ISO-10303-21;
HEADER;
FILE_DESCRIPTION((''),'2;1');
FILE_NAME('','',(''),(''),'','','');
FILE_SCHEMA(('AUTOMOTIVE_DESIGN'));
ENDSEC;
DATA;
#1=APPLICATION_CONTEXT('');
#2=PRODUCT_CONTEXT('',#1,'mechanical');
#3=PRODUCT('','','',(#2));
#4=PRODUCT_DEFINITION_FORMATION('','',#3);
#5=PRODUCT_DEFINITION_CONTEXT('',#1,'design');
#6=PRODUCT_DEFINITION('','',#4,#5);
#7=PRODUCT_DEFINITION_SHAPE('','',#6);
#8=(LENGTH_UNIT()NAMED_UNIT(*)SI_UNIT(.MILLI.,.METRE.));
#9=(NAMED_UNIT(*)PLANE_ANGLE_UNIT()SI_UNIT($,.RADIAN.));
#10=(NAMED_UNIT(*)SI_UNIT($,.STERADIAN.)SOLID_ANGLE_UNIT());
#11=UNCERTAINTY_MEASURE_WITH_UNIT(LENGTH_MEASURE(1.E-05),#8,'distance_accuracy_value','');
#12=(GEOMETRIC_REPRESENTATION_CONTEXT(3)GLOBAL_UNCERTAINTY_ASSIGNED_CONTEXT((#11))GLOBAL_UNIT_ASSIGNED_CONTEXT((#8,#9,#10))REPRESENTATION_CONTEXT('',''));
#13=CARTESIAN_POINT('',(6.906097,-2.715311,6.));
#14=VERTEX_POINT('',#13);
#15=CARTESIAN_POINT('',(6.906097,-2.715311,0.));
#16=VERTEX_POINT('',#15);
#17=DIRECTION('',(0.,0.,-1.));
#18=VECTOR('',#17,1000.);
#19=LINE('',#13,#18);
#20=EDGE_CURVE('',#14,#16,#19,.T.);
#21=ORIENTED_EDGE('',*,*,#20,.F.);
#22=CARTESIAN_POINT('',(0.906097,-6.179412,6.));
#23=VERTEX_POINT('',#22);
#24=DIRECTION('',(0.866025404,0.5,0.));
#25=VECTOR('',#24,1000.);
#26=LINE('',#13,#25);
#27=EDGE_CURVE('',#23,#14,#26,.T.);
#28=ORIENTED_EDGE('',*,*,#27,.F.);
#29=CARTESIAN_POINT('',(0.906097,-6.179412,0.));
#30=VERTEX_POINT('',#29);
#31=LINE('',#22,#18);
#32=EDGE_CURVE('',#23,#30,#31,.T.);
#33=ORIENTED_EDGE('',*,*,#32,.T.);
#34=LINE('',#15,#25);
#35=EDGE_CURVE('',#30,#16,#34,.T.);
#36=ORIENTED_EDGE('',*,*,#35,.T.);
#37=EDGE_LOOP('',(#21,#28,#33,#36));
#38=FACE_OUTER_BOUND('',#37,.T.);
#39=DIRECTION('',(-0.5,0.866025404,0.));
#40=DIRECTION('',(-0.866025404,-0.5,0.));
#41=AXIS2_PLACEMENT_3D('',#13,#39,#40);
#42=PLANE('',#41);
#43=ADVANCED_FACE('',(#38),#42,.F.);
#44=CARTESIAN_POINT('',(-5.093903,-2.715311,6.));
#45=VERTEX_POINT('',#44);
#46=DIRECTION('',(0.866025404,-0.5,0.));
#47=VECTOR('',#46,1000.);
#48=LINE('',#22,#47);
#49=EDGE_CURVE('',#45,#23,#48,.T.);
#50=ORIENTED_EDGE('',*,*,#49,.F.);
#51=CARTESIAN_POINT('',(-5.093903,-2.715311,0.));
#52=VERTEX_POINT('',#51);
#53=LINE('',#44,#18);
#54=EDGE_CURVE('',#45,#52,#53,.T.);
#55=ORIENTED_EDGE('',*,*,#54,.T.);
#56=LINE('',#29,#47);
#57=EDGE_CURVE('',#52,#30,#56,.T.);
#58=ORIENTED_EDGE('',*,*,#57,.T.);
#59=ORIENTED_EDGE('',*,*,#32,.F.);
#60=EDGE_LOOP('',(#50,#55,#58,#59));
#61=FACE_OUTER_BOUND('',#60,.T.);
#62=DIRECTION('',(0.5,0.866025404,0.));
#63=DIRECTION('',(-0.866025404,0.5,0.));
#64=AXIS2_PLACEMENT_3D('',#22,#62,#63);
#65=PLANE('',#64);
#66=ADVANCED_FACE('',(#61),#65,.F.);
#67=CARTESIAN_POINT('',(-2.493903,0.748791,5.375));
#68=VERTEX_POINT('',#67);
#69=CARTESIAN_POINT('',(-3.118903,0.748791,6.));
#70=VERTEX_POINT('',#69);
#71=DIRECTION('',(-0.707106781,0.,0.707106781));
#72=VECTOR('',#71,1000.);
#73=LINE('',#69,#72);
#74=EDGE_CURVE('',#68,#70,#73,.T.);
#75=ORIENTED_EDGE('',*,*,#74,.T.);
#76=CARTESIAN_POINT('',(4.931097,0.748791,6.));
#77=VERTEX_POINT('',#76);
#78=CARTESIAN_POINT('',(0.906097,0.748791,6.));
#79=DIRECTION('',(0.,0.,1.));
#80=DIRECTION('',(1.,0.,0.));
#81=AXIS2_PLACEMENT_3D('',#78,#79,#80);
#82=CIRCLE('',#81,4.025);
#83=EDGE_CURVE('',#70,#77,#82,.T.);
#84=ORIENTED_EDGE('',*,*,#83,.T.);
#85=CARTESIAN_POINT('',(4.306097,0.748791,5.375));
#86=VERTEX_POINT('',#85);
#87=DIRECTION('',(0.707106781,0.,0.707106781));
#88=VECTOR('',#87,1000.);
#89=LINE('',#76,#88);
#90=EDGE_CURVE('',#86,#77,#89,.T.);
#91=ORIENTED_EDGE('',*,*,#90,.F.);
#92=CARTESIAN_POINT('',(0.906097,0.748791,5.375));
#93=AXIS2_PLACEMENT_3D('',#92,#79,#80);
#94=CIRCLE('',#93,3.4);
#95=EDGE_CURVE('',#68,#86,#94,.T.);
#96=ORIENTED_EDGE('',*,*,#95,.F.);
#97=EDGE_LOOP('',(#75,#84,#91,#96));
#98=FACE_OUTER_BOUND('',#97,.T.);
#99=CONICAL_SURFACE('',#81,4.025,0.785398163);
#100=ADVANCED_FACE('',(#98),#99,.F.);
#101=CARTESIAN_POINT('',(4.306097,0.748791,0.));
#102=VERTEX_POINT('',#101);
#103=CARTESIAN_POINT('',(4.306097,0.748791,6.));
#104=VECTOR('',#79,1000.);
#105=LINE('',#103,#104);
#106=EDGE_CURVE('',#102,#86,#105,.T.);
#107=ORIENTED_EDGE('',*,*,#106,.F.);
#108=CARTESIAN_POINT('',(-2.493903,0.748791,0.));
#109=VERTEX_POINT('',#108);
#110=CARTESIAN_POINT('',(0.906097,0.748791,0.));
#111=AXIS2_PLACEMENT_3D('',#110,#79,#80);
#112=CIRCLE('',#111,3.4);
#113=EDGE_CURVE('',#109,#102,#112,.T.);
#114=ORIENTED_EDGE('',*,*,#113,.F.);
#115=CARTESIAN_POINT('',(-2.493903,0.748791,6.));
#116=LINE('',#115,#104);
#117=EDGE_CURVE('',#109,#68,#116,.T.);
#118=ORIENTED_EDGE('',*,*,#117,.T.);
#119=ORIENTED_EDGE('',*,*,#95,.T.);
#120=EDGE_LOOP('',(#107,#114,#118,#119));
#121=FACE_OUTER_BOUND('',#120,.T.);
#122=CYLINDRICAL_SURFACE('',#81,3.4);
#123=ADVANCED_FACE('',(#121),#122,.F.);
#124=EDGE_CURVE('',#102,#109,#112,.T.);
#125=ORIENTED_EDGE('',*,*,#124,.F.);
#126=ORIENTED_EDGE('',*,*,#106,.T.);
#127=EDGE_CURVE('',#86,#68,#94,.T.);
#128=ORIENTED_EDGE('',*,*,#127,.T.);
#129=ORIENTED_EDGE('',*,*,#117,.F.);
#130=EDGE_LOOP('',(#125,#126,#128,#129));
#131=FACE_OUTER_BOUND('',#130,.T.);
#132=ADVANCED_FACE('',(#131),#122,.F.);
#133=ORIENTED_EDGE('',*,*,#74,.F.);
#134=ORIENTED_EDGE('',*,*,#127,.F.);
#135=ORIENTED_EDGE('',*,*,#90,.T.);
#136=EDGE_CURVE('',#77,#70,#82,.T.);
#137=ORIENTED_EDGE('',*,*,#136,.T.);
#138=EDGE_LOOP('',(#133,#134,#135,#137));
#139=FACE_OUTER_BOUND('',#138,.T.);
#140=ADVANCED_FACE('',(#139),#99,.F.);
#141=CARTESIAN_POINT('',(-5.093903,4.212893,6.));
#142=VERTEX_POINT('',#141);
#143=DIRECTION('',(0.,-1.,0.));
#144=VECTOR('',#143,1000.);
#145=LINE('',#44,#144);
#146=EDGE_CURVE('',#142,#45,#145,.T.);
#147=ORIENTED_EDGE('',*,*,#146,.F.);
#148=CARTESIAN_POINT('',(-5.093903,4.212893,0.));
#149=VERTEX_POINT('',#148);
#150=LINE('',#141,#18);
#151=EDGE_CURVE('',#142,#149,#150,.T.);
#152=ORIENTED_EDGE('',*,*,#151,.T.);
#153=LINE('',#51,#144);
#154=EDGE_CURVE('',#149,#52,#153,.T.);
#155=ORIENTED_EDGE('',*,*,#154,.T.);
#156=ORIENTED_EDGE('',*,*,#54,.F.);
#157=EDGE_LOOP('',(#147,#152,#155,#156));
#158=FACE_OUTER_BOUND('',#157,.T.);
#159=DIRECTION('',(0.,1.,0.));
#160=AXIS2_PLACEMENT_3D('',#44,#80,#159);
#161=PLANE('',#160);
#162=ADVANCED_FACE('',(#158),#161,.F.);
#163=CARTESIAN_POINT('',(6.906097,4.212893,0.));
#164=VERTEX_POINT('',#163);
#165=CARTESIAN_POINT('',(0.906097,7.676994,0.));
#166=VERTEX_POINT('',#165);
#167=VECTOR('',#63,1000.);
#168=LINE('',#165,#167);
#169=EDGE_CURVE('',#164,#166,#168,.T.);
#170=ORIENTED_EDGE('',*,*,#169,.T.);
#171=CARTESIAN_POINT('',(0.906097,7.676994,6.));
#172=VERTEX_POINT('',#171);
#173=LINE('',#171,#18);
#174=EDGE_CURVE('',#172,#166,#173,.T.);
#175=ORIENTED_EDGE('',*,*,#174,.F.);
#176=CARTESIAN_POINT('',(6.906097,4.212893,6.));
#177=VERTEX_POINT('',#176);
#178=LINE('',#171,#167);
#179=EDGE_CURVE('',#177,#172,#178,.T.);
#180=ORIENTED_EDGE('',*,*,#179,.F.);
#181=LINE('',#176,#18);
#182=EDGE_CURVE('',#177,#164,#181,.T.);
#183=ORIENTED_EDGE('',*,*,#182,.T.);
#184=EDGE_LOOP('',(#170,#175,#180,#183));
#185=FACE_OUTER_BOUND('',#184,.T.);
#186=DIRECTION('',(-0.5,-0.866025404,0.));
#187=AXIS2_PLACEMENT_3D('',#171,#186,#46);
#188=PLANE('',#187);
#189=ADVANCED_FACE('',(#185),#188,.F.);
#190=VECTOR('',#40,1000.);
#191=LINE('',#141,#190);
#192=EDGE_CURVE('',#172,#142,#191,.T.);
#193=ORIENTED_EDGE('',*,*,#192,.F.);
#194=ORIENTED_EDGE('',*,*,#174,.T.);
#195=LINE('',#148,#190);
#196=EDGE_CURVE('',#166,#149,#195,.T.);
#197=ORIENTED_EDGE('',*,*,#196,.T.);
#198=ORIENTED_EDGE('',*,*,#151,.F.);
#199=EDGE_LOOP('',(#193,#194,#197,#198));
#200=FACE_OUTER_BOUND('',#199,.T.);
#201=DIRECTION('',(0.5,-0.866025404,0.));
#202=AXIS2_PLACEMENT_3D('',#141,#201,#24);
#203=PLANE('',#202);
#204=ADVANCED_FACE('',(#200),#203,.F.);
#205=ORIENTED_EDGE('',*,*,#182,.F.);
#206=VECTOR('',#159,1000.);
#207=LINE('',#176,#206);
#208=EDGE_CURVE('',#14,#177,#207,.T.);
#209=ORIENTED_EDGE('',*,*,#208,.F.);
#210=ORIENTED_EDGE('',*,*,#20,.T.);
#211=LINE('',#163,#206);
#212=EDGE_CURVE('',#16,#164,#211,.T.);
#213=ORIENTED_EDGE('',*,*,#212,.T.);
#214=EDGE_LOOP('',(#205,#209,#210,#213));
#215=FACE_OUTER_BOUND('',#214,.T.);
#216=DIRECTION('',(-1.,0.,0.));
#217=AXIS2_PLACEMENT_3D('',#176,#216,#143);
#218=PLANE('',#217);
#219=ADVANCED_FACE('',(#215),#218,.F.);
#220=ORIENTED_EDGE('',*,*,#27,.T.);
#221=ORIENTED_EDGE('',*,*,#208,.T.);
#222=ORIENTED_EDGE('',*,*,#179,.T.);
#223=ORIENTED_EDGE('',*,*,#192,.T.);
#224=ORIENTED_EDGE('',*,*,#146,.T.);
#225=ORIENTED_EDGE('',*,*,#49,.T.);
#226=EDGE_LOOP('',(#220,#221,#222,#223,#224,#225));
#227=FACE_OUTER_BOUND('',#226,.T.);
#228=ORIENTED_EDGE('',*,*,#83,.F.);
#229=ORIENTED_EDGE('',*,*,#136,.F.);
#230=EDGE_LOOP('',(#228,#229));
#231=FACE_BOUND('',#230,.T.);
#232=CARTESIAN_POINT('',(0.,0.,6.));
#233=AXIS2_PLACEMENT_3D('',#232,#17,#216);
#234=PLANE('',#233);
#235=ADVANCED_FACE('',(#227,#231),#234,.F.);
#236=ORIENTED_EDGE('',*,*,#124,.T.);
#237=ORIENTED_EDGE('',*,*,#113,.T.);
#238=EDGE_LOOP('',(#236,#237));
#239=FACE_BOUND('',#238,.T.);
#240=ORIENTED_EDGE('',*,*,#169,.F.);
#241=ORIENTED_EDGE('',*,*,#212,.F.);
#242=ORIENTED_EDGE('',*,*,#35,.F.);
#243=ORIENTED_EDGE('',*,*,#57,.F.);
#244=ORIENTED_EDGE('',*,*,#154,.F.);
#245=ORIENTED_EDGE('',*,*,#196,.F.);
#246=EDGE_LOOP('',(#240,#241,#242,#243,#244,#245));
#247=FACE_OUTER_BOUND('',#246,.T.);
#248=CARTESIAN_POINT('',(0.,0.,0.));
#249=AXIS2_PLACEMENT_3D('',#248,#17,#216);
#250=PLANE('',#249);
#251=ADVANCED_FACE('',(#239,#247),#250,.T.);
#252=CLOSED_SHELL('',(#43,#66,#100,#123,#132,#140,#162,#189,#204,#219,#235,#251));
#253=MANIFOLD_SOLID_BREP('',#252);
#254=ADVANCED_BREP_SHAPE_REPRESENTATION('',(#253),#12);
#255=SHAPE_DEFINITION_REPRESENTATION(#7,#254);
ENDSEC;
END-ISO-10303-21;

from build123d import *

# Parameters (mm, degrees)
BOSS_EXTRUDE1_DEPTH         = 6
M8_TAPPED_HOLE1_D           = 6.8
M8_TAPPED_HOLE1_CSINK_D     = 8.05
M8_TAPPED_HOLE1_CSINK_ANGLE = 90


with BuildPart() as part:
    # Sketch1 → Boss-Extrude1 (new body)
    with BuildSketch(Plane.XY):
        Polygon((-5.093902669, -2.715310597), (-5.093902669, 4.212892633), (0.906097331, 7.676994248), (6.906097331, 4.212892633), (6.906097331, -2.715310597), (0.906097331, -6.179412212), align=None)
    extrude(amount=BOSS_EXTRUDE1_DEPTH)

    # M8 Tapped Hole1 (through all)
    with Locations(Plane.XY.offset(6)):
        with Locations((0.906097331, 0.748791018)):
            CounterSinkHole(M8_TAPPED_HOLE1_D / 2, M8_TAPPED_HOLE1_CSINK_D / 2, counter_sink_angle=M8_TAPPED_HOLE1_CSINK_ANGLE)


solid = part.part
